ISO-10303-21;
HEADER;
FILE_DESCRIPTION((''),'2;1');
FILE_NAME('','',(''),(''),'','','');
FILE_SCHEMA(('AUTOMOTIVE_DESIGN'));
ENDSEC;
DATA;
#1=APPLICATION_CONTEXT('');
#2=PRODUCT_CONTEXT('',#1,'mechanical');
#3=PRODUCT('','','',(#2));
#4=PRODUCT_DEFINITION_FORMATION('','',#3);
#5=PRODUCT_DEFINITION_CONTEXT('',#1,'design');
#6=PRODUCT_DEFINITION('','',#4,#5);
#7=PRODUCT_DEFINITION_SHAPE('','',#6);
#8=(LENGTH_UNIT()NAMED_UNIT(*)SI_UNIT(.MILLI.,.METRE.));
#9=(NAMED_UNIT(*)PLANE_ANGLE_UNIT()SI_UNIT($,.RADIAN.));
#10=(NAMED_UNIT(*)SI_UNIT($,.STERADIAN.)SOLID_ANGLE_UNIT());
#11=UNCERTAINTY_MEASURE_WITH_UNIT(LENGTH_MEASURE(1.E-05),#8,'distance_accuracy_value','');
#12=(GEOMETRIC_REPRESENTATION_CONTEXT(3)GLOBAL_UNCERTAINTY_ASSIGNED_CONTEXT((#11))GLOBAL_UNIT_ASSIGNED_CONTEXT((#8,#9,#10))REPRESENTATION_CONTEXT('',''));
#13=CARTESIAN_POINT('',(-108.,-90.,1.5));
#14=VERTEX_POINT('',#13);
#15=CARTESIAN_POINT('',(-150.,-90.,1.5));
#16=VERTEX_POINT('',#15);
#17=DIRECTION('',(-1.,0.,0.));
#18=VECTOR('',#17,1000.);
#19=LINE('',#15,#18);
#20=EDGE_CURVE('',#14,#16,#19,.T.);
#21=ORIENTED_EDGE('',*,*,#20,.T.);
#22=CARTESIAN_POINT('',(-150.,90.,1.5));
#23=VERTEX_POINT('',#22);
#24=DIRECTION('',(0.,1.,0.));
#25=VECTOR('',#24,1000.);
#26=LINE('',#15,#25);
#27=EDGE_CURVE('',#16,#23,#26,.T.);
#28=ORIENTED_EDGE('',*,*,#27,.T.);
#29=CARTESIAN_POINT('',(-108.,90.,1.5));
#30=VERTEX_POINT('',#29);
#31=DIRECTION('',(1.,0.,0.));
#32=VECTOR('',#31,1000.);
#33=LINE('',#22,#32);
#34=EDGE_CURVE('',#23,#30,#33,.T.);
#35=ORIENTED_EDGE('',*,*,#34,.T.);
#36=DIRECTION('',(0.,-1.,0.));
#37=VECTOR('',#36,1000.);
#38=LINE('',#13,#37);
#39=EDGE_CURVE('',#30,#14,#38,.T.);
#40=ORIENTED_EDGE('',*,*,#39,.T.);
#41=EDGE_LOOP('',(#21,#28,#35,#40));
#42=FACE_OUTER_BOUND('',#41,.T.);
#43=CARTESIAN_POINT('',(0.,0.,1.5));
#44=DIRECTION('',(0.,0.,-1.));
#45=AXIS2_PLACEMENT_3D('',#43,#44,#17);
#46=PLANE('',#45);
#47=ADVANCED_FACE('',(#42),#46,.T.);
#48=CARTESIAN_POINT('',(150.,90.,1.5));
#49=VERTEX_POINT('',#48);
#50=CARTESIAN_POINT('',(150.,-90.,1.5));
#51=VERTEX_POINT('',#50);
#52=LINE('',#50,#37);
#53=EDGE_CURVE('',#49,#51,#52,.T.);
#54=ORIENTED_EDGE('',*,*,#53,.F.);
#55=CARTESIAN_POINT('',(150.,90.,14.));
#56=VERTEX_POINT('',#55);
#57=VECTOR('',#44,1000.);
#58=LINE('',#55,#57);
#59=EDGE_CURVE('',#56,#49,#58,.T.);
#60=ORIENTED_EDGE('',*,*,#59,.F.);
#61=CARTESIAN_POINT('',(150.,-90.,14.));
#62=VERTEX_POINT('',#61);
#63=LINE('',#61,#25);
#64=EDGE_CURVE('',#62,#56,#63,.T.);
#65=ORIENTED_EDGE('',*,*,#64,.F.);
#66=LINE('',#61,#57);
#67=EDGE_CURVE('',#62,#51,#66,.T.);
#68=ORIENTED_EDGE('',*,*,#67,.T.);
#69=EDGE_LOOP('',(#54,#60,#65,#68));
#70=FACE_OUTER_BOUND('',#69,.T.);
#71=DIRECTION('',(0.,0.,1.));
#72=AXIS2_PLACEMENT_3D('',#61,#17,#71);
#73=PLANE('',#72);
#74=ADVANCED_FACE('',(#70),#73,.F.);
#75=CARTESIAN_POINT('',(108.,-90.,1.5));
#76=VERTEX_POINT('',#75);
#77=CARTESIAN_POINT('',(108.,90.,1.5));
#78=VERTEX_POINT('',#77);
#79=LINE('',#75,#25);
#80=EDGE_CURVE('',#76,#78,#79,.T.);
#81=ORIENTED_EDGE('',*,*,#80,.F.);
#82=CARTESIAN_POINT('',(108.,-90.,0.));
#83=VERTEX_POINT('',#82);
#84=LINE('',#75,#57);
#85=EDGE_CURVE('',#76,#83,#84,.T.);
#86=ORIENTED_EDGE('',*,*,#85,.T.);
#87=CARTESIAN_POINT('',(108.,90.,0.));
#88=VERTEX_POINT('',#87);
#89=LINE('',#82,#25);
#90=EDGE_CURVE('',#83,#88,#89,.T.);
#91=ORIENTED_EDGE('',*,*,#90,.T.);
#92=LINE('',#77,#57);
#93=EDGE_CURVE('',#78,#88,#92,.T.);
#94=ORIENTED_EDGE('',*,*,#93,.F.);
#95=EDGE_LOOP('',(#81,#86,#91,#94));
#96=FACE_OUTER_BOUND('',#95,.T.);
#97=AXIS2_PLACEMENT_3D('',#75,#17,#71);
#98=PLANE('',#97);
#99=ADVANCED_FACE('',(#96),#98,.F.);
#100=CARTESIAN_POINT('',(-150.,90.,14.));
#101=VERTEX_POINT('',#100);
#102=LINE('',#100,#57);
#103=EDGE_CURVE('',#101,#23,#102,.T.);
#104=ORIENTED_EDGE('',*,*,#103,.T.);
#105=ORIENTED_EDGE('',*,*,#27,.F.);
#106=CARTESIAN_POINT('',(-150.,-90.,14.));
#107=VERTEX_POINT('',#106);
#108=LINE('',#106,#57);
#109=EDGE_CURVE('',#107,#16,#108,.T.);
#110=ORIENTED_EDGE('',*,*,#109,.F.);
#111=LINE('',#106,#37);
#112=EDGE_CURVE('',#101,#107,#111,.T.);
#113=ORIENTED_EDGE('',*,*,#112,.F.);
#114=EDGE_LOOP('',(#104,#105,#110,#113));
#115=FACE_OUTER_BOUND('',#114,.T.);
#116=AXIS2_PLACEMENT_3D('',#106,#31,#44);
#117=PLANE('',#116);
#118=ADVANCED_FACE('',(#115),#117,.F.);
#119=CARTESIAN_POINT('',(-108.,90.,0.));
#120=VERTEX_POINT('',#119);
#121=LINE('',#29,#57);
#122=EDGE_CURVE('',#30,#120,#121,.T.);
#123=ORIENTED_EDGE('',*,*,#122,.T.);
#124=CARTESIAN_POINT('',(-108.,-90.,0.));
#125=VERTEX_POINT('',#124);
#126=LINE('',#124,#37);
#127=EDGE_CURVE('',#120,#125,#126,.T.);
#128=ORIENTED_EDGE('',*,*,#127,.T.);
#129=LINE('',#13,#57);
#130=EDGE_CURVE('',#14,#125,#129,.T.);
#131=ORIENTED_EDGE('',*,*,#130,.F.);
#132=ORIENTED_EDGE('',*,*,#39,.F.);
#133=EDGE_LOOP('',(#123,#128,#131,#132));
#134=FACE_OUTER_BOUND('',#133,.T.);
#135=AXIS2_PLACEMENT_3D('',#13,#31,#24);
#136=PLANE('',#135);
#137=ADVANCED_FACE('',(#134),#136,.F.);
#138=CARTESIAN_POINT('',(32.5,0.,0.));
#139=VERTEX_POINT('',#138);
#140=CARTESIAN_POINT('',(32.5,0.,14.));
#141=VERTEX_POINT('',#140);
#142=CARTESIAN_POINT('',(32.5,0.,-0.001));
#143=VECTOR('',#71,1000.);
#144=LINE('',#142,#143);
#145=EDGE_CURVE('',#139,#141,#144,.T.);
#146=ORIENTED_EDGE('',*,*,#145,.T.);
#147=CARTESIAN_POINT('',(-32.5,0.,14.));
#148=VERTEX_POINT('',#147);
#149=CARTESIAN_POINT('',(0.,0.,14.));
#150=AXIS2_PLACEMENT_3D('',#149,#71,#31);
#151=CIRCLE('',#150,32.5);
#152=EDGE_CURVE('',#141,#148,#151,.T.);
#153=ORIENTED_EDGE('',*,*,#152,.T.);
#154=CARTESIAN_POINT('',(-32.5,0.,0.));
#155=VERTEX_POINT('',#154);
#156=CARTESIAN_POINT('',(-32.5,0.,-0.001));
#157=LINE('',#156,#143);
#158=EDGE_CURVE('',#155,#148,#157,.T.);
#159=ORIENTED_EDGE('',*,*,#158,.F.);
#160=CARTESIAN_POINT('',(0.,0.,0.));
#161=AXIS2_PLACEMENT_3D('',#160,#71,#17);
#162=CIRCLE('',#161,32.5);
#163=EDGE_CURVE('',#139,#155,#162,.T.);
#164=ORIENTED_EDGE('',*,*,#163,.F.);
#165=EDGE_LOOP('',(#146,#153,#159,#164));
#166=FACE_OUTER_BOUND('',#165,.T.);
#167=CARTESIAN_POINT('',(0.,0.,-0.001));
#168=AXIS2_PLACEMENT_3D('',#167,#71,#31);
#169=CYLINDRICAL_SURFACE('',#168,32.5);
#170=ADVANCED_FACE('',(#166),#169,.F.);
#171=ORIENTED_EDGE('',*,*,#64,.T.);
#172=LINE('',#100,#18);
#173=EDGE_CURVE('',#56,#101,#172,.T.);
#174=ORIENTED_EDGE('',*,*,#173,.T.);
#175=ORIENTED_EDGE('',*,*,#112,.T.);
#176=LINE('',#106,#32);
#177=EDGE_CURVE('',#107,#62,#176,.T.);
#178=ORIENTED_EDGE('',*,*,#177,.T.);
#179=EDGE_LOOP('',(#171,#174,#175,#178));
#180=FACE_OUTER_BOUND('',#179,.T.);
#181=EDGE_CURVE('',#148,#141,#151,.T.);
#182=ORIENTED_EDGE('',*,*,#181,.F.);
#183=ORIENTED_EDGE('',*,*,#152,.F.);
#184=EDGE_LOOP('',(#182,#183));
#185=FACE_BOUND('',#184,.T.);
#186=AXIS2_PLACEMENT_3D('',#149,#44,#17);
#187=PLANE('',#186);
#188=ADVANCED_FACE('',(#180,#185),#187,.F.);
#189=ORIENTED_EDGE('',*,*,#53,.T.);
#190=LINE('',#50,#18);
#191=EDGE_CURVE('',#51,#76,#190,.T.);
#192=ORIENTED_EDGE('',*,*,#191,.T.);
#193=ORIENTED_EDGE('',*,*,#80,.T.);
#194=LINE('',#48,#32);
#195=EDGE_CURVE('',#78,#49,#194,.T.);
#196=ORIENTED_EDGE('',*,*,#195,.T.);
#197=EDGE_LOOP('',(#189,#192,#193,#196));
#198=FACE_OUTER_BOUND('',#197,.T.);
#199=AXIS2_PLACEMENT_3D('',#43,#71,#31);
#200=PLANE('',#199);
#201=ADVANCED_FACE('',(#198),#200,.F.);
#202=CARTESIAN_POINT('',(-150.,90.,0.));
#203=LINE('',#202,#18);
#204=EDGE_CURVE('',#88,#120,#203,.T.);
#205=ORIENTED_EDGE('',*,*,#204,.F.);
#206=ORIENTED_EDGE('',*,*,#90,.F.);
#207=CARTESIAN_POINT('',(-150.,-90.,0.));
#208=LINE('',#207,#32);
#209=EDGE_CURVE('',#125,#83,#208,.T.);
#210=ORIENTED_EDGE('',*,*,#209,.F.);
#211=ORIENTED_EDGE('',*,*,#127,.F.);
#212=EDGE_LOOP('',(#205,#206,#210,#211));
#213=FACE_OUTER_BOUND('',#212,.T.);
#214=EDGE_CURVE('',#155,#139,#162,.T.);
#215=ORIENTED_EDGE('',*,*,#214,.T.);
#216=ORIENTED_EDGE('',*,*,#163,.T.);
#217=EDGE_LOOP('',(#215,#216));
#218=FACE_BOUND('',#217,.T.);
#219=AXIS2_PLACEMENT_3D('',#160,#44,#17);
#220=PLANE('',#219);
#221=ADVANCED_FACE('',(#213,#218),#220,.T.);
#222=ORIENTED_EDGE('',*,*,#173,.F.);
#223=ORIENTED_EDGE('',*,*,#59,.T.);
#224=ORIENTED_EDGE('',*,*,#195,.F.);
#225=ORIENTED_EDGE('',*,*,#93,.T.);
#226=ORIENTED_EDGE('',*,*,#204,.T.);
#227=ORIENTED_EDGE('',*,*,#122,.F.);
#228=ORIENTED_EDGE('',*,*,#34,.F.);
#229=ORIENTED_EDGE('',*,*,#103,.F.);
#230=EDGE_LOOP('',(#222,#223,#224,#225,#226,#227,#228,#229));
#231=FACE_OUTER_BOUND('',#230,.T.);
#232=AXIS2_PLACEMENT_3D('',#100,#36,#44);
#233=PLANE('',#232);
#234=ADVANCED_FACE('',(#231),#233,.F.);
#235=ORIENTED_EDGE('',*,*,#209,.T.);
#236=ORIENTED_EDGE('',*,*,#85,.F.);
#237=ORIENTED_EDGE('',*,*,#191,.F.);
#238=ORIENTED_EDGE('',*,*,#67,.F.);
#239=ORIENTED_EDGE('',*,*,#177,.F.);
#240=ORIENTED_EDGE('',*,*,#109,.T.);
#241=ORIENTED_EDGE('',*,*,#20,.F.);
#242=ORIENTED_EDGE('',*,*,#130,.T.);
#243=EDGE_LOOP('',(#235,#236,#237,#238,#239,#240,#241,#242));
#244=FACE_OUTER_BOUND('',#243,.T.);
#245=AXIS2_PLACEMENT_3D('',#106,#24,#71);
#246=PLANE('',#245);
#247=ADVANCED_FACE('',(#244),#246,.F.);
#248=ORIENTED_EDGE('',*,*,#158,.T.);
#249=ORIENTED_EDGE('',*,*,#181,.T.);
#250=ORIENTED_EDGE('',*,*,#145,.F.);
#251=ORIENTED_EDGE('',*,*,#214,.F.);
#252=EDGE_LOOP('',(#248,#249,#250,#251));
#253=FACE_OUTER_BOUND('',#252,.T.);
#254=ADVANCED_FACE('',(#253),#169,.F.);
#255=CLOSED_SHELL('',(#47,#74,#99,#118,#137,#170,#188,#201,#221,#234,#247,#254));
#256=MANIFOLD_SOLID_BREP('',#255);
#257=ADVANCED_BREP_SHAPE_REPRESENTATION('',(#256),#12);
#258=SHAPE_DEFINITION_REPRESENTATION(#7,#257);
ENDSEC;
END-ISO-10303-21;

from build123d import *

# Parameters (mm, degrees)
SKETCH_1_W          = 300
SKETCH_1_H          = 180
EXTRUDE_1_DEPTH     = 14
SKETCH_2_W          = 42
SKETCH_2_H          = 180
CUT_EXTRUDE_1_DEPTH = 1.5
CUT_EXTRUDE_2_REACH = 177.488
SKETCH_3_R          = 32.5


with BuildPart() as part:
    # 草图1 → 凸台-拉伸1 (new body)
    with BuildSketch(Plane.XY):
        Rectangle(SKETCH_1_W, SKETCH_1_H)
    extrude(amount=EXTRUDE_1_DEPTH)

    # 草图2 → 切除-拉伸1 (cut)
    with BuildSketch(Plane(origin=(0, 0, 0), x_dir=(-1, 0, 0), z_dir=(0, 0, -1))):
        with Locations((129, 0)):
            Rectangle(SKETCH_2_W, SKETCH_2_H)
        with Locations((-129, 0)):
            Rectangle(SKETCH_2_W, SKETCH_2_H)
    extrude(amount=-CUT_EXTRUDE_1_DEPTH, mode=Mode.SUBTRACT)

    # 草图3 → 切除-拉伸2 (cut, up to next)
    with BuildSketch(Plane.XY.offset(14), mode=Mode.PRIVATE) as cut_extrude_2_sk1:
        Circle(SKETCH_3_R)
    cut_extrude_2_tool1 = extrude(cut_extrude_2_sk1.sketch, amount=-CUT_EXTRUDE_2_REACH, mode=Mode.PRIVATE) & part.part
    add(cut_extrude_2_tool1.solids().sort_by_distance((0, 0, 14))[0], mode=Mode.SUBTRACT)


solid = part.part
